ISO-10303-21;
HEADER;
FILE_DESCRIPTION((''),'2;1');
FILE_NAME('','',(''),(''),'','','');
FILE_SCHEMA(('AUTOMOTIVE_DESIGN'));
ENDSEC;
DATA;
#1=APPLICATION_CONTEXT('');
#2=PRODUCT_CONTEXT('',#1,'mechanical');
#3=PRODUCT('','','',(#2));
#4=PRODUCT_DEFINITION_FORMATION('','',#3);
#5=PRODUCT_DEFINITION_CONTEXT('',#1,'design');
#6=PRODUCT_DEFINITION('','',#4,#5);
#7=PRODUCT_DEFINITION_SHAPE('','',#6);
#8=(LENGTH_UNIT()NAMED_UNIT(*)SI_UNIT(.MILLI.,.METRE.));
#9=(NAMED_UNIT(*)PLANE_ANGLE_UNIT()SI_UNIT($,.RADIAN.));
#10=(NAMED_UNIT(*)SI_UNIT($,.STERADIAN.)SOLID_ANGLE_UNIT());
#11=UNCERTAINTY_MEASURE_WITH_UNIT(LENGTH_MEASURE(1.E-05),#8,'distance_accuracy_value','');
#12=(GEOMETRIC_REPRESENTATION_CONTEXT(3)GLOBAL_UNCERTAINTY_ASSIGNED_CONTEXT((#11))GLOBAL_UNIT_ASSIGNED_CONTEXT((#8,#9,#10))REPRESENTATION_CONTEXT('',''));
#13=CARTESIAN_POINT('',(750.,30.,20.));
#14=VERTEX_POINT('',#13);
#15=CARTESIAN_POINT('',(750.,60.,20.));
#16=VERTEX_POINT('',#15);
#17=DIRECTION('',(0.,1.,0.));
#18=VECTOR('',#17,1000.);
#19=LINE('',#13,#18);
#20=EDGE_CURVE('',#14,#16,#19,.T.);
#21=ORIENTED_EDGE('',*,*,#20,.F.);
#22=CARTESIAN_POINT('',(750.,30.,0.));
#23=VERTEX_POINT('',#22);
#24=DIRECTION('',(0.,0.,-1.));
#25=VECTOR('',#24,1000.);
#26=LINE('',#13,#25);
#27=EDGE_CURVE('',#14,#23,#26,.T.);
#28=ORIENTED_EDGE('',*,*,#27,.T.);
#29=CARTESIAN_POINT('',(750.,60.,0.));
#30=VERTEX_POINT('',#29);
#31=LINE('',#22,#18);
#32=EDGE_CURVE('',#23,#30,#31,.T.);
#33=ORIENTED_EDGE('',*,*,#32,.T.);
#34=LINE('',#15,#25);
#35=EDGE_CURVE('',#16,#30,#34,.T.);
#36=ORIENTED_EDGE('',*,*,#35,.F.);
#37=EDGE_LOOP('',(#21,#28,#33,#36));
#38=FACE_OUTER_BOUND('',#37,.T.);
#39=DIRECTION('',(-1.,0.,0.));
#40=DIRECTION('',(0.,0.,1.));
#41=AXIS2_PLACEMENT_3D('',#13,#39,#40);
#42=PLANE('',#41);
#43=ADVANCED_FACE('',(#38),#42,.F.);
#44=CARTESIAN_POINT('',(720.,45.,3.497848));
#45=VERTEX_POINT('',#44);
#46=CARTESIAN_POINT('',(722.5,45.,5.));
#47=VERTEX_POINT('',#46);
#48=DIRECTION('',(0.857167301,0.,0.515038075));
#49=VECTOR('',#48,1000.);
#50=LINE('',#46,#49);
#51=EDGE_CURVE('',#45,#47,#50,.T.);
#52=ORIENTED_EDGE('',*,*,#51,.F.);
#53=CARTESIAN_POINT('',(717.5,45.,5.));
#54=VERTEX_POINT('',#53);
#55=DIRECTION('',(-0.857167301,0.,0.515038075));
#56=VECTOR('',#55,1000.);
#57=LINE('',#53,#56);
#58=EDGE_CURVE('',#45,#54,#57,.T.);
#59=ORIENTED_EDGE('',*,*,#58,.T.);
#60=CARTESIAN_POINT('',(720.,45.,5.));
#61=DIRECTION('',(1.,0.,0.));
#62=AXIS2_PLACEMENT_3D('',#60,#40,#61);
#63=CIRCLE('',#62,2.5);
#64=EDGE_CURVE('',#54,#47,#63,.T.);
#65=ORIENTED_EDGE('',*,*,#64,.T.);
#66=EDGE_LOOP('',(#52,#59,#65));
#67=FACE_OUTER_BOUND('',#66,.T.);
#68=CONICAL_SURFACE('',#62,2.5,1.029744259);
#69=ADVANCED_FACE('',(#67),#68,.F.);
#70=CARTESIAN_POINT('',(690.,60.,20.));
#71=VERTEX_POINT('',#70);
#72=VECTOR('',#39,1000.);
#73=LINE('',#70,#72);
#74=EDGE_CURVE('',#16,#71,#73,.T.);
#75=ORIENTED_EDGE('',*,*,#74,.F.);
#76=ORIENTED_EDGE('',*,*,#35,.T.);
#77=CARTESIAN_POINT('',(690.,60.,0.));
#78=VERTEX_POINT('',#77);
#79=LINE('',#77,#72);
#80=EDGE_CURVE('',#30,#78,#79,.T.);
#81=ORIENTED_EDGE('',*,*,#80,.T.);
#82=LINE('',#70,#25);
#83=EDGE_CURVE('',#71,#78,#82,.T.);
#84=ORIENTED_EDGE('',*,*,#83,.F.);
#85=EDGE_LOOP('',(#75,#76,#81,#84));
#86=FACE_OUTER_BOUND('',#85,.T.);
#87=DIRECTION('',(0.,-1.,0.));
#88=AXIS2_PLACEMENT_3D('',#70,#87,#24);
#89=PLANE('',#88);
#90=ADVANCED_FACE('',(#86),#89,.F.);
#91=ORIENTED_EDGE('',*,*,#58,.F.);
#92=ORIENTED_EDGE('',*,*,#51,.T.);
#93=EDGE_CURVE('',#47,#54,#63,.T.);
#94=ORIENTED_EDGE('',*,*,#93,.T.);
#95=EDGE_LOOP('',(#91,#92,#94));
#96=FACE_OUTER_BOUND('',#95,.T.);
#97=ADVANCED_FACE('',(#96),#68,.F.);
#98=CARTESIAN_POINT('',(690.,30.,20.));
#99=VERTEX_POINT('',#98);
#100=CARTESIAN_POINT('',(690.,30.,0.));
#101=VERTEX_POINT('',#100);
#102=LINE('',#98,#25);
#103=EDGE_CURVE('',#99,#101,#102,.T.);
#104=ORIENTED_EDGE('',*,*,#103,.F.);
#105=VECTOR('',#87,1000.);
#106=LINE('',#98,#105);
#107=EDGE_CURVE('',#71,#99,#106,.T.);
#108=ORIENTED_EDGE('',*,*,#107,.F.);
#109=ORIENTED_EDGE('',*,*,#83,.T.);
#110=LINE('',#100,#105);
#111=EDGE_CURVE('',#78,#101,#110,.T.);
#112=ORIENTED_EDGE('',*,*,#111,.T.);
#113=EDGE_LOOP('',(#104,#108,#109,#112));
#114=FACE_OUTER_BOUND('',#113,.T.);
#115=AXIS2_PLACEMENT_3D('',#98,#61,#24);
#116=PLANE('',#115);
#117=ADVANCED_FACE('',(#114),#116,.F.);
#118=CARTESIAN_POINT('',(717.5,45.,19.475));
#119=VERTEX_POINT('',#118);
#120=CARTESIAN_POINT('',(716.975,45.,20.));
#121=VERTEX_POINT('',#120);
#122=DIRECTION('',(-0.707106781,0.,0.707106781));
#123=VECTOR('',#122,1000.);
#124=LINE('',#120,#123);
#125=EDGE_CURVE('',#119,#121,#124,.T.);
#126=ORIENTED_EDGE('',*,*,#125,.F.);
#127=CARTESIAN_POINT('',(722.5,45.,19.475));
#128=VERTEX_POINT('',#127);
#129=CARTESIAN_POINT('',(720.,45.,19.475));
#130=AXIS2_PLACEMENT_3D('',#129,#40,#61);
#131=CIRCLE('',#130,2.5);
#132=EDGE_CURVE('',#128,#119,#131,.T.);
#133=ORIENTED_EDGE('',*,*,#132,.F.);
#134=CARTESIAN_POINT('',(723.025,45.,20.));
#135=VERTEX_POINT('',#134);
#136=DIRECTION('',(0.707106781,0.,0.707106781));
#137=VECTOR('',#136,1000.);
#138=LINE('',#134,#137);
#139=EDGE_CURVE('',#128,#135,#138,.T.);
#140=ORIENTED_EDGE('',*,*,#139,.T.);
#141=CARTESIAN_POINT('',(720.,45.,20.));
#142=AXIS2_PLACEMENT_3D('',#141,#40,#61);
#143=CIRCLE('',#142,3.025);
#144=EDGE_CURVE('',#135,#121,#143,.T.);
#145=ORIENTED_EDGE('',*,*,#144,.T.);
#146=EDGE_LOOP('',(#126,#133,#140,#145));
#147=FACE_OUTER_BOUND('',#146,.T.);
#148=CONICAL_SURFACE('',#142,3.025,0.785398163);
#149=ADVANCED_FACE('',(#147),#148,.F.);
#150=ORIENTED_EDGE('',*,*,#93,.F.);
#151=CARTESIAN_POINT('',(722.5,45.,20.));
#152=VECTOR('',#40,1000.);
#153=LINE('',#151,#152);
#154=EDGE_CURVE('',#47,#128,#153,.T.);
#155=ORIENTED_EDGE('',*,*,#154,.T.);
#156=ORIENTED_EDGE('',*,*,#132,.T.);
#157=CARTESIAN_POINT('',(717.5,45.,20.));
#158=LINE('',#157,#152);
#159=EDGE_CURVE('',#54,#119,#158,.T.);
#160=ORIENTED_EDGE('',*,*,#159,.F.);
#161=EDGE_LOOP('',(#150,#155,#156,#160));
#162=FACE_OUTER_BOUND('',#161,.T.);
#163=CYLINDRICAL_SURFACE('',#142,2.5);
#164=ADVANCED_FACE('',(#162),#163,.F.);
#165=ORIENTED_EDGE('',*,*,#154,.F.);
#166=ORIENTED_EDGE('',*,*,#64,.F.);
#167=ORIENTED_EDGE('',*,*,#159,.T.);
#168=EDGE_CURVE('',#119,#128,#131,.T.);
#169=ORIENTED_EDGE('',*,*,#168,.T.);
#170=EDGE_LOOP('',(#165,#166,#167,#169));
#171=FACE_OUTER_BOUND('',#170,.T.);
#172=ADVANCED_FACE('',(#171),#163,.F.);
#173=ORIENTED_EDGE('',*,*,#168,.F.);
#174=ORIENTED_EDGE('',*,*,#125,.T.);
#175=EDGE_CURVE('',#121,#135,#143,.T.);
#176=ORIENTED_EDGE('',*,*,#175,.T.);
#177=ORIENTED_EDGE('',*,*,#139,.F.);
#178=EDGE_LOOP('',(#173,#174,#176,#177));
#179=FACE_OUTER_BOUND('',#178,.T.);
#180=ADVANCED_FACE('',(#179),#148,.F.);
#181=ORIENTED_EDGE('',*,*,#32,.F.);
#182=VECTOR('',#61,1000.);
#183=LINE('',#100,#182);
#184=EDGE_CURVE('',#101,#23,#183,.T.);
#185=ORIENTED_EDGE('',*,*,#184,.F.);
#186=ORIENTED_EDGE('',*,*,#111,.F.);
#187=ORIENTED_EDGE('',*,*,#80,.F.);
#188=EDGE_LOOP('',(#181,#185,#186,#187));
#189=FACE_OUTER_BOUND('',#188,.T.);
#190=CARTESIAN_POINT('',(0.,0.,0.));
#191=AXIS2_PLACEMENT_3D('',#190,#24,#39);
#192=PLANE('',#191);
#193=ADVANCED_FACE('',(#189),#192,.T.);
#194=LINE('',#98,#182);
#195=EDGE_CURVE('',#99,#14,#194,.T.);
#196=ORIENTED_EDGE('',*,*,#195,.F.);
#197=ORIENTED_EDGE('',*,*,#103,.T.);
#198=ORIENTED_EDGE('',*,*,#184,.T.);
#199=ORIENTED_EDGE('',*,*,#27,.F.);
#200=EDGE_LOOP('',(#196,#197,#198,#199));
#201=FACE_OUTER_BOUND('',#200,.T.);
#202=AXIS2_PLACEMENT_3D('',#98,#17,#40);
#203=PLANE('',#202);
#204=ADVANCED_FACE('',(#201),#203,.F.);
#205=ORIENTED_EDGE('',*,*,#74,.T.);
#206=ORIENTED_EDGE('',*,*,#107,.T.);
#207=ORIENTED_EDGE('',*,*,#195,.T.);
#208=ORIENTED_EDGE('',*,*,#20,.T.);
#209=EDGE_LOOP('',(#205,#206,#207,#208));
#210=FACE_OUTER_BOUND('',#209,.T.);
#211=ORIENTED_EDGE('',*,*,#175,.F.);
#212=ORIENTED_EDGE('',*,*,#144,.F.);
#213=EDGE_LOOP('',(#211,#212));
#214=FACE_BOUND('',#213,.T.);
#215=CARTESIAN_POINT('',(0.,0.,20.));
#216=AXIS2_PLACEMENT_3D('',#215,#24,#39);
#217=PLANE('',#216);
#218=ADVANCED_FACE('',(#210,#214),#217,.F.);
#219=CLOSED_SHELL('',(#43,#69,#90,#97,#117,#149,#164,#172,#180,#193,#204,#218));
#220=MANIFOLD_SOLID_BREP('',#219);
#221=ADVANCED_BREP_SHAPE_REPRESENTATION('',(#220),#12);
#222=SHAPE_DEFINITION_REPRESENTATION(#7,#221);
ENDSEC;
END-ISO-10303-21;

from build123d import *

# Parameters (mm, degrees)
SKETCH1_W                   = 60
SKETCH1_H                   = 30
BOSS_EXTRUDE1_DEPTH         = 20
M6_TAPPED_HOLE1_D           = 5
M6_TAPPED_HOLE1_DEPTH       = 15
M6_TAPPED_HOLE1_CSINK_D     = 6.05
M6_TAPPED_HOLE1_CSINK_ANGLE = 90
M6_TAPPED_HOLE1_TIP         = 1.502151548


with BuildPart() as part:
    # Sketch1 → Boss-Extrude1 (new body)
    with BuildSketch(Plane.XY):
        with Locations((720, 45)):
            Rectangle(SKETCH1_W, SKETCH1_H)
    extrude(amount=BOSS_EXTRUDE1_DEPTH)

    # M6 Tapped Hole1
    with Locations(Plane.XY.offset(20)):
        with Locations((720, 45)):
            CounterSinkHole(M6_TAPPED_HOLE1_D / 2, M6_TAPPED_HOLE1_CSINK_D / 2, depth=M6_TAPPED_HOLE1_DEPTH, counter_sink_angle=M6_TAPPED_HOLE1_CSINK_ANGLE)
            with Locations((0, 0, -(M6_TAPPED_HOLE1_DEPTH + M6_TAPPED_HOLE1_TIP / 2))):  # 118° drill point
                Cone(0, M6_TAPPED_HOLE1_D / 2, M6_TAPPED_HOLE1_TIP, mode=Mode.SUBTRACT)


solid = part.part
